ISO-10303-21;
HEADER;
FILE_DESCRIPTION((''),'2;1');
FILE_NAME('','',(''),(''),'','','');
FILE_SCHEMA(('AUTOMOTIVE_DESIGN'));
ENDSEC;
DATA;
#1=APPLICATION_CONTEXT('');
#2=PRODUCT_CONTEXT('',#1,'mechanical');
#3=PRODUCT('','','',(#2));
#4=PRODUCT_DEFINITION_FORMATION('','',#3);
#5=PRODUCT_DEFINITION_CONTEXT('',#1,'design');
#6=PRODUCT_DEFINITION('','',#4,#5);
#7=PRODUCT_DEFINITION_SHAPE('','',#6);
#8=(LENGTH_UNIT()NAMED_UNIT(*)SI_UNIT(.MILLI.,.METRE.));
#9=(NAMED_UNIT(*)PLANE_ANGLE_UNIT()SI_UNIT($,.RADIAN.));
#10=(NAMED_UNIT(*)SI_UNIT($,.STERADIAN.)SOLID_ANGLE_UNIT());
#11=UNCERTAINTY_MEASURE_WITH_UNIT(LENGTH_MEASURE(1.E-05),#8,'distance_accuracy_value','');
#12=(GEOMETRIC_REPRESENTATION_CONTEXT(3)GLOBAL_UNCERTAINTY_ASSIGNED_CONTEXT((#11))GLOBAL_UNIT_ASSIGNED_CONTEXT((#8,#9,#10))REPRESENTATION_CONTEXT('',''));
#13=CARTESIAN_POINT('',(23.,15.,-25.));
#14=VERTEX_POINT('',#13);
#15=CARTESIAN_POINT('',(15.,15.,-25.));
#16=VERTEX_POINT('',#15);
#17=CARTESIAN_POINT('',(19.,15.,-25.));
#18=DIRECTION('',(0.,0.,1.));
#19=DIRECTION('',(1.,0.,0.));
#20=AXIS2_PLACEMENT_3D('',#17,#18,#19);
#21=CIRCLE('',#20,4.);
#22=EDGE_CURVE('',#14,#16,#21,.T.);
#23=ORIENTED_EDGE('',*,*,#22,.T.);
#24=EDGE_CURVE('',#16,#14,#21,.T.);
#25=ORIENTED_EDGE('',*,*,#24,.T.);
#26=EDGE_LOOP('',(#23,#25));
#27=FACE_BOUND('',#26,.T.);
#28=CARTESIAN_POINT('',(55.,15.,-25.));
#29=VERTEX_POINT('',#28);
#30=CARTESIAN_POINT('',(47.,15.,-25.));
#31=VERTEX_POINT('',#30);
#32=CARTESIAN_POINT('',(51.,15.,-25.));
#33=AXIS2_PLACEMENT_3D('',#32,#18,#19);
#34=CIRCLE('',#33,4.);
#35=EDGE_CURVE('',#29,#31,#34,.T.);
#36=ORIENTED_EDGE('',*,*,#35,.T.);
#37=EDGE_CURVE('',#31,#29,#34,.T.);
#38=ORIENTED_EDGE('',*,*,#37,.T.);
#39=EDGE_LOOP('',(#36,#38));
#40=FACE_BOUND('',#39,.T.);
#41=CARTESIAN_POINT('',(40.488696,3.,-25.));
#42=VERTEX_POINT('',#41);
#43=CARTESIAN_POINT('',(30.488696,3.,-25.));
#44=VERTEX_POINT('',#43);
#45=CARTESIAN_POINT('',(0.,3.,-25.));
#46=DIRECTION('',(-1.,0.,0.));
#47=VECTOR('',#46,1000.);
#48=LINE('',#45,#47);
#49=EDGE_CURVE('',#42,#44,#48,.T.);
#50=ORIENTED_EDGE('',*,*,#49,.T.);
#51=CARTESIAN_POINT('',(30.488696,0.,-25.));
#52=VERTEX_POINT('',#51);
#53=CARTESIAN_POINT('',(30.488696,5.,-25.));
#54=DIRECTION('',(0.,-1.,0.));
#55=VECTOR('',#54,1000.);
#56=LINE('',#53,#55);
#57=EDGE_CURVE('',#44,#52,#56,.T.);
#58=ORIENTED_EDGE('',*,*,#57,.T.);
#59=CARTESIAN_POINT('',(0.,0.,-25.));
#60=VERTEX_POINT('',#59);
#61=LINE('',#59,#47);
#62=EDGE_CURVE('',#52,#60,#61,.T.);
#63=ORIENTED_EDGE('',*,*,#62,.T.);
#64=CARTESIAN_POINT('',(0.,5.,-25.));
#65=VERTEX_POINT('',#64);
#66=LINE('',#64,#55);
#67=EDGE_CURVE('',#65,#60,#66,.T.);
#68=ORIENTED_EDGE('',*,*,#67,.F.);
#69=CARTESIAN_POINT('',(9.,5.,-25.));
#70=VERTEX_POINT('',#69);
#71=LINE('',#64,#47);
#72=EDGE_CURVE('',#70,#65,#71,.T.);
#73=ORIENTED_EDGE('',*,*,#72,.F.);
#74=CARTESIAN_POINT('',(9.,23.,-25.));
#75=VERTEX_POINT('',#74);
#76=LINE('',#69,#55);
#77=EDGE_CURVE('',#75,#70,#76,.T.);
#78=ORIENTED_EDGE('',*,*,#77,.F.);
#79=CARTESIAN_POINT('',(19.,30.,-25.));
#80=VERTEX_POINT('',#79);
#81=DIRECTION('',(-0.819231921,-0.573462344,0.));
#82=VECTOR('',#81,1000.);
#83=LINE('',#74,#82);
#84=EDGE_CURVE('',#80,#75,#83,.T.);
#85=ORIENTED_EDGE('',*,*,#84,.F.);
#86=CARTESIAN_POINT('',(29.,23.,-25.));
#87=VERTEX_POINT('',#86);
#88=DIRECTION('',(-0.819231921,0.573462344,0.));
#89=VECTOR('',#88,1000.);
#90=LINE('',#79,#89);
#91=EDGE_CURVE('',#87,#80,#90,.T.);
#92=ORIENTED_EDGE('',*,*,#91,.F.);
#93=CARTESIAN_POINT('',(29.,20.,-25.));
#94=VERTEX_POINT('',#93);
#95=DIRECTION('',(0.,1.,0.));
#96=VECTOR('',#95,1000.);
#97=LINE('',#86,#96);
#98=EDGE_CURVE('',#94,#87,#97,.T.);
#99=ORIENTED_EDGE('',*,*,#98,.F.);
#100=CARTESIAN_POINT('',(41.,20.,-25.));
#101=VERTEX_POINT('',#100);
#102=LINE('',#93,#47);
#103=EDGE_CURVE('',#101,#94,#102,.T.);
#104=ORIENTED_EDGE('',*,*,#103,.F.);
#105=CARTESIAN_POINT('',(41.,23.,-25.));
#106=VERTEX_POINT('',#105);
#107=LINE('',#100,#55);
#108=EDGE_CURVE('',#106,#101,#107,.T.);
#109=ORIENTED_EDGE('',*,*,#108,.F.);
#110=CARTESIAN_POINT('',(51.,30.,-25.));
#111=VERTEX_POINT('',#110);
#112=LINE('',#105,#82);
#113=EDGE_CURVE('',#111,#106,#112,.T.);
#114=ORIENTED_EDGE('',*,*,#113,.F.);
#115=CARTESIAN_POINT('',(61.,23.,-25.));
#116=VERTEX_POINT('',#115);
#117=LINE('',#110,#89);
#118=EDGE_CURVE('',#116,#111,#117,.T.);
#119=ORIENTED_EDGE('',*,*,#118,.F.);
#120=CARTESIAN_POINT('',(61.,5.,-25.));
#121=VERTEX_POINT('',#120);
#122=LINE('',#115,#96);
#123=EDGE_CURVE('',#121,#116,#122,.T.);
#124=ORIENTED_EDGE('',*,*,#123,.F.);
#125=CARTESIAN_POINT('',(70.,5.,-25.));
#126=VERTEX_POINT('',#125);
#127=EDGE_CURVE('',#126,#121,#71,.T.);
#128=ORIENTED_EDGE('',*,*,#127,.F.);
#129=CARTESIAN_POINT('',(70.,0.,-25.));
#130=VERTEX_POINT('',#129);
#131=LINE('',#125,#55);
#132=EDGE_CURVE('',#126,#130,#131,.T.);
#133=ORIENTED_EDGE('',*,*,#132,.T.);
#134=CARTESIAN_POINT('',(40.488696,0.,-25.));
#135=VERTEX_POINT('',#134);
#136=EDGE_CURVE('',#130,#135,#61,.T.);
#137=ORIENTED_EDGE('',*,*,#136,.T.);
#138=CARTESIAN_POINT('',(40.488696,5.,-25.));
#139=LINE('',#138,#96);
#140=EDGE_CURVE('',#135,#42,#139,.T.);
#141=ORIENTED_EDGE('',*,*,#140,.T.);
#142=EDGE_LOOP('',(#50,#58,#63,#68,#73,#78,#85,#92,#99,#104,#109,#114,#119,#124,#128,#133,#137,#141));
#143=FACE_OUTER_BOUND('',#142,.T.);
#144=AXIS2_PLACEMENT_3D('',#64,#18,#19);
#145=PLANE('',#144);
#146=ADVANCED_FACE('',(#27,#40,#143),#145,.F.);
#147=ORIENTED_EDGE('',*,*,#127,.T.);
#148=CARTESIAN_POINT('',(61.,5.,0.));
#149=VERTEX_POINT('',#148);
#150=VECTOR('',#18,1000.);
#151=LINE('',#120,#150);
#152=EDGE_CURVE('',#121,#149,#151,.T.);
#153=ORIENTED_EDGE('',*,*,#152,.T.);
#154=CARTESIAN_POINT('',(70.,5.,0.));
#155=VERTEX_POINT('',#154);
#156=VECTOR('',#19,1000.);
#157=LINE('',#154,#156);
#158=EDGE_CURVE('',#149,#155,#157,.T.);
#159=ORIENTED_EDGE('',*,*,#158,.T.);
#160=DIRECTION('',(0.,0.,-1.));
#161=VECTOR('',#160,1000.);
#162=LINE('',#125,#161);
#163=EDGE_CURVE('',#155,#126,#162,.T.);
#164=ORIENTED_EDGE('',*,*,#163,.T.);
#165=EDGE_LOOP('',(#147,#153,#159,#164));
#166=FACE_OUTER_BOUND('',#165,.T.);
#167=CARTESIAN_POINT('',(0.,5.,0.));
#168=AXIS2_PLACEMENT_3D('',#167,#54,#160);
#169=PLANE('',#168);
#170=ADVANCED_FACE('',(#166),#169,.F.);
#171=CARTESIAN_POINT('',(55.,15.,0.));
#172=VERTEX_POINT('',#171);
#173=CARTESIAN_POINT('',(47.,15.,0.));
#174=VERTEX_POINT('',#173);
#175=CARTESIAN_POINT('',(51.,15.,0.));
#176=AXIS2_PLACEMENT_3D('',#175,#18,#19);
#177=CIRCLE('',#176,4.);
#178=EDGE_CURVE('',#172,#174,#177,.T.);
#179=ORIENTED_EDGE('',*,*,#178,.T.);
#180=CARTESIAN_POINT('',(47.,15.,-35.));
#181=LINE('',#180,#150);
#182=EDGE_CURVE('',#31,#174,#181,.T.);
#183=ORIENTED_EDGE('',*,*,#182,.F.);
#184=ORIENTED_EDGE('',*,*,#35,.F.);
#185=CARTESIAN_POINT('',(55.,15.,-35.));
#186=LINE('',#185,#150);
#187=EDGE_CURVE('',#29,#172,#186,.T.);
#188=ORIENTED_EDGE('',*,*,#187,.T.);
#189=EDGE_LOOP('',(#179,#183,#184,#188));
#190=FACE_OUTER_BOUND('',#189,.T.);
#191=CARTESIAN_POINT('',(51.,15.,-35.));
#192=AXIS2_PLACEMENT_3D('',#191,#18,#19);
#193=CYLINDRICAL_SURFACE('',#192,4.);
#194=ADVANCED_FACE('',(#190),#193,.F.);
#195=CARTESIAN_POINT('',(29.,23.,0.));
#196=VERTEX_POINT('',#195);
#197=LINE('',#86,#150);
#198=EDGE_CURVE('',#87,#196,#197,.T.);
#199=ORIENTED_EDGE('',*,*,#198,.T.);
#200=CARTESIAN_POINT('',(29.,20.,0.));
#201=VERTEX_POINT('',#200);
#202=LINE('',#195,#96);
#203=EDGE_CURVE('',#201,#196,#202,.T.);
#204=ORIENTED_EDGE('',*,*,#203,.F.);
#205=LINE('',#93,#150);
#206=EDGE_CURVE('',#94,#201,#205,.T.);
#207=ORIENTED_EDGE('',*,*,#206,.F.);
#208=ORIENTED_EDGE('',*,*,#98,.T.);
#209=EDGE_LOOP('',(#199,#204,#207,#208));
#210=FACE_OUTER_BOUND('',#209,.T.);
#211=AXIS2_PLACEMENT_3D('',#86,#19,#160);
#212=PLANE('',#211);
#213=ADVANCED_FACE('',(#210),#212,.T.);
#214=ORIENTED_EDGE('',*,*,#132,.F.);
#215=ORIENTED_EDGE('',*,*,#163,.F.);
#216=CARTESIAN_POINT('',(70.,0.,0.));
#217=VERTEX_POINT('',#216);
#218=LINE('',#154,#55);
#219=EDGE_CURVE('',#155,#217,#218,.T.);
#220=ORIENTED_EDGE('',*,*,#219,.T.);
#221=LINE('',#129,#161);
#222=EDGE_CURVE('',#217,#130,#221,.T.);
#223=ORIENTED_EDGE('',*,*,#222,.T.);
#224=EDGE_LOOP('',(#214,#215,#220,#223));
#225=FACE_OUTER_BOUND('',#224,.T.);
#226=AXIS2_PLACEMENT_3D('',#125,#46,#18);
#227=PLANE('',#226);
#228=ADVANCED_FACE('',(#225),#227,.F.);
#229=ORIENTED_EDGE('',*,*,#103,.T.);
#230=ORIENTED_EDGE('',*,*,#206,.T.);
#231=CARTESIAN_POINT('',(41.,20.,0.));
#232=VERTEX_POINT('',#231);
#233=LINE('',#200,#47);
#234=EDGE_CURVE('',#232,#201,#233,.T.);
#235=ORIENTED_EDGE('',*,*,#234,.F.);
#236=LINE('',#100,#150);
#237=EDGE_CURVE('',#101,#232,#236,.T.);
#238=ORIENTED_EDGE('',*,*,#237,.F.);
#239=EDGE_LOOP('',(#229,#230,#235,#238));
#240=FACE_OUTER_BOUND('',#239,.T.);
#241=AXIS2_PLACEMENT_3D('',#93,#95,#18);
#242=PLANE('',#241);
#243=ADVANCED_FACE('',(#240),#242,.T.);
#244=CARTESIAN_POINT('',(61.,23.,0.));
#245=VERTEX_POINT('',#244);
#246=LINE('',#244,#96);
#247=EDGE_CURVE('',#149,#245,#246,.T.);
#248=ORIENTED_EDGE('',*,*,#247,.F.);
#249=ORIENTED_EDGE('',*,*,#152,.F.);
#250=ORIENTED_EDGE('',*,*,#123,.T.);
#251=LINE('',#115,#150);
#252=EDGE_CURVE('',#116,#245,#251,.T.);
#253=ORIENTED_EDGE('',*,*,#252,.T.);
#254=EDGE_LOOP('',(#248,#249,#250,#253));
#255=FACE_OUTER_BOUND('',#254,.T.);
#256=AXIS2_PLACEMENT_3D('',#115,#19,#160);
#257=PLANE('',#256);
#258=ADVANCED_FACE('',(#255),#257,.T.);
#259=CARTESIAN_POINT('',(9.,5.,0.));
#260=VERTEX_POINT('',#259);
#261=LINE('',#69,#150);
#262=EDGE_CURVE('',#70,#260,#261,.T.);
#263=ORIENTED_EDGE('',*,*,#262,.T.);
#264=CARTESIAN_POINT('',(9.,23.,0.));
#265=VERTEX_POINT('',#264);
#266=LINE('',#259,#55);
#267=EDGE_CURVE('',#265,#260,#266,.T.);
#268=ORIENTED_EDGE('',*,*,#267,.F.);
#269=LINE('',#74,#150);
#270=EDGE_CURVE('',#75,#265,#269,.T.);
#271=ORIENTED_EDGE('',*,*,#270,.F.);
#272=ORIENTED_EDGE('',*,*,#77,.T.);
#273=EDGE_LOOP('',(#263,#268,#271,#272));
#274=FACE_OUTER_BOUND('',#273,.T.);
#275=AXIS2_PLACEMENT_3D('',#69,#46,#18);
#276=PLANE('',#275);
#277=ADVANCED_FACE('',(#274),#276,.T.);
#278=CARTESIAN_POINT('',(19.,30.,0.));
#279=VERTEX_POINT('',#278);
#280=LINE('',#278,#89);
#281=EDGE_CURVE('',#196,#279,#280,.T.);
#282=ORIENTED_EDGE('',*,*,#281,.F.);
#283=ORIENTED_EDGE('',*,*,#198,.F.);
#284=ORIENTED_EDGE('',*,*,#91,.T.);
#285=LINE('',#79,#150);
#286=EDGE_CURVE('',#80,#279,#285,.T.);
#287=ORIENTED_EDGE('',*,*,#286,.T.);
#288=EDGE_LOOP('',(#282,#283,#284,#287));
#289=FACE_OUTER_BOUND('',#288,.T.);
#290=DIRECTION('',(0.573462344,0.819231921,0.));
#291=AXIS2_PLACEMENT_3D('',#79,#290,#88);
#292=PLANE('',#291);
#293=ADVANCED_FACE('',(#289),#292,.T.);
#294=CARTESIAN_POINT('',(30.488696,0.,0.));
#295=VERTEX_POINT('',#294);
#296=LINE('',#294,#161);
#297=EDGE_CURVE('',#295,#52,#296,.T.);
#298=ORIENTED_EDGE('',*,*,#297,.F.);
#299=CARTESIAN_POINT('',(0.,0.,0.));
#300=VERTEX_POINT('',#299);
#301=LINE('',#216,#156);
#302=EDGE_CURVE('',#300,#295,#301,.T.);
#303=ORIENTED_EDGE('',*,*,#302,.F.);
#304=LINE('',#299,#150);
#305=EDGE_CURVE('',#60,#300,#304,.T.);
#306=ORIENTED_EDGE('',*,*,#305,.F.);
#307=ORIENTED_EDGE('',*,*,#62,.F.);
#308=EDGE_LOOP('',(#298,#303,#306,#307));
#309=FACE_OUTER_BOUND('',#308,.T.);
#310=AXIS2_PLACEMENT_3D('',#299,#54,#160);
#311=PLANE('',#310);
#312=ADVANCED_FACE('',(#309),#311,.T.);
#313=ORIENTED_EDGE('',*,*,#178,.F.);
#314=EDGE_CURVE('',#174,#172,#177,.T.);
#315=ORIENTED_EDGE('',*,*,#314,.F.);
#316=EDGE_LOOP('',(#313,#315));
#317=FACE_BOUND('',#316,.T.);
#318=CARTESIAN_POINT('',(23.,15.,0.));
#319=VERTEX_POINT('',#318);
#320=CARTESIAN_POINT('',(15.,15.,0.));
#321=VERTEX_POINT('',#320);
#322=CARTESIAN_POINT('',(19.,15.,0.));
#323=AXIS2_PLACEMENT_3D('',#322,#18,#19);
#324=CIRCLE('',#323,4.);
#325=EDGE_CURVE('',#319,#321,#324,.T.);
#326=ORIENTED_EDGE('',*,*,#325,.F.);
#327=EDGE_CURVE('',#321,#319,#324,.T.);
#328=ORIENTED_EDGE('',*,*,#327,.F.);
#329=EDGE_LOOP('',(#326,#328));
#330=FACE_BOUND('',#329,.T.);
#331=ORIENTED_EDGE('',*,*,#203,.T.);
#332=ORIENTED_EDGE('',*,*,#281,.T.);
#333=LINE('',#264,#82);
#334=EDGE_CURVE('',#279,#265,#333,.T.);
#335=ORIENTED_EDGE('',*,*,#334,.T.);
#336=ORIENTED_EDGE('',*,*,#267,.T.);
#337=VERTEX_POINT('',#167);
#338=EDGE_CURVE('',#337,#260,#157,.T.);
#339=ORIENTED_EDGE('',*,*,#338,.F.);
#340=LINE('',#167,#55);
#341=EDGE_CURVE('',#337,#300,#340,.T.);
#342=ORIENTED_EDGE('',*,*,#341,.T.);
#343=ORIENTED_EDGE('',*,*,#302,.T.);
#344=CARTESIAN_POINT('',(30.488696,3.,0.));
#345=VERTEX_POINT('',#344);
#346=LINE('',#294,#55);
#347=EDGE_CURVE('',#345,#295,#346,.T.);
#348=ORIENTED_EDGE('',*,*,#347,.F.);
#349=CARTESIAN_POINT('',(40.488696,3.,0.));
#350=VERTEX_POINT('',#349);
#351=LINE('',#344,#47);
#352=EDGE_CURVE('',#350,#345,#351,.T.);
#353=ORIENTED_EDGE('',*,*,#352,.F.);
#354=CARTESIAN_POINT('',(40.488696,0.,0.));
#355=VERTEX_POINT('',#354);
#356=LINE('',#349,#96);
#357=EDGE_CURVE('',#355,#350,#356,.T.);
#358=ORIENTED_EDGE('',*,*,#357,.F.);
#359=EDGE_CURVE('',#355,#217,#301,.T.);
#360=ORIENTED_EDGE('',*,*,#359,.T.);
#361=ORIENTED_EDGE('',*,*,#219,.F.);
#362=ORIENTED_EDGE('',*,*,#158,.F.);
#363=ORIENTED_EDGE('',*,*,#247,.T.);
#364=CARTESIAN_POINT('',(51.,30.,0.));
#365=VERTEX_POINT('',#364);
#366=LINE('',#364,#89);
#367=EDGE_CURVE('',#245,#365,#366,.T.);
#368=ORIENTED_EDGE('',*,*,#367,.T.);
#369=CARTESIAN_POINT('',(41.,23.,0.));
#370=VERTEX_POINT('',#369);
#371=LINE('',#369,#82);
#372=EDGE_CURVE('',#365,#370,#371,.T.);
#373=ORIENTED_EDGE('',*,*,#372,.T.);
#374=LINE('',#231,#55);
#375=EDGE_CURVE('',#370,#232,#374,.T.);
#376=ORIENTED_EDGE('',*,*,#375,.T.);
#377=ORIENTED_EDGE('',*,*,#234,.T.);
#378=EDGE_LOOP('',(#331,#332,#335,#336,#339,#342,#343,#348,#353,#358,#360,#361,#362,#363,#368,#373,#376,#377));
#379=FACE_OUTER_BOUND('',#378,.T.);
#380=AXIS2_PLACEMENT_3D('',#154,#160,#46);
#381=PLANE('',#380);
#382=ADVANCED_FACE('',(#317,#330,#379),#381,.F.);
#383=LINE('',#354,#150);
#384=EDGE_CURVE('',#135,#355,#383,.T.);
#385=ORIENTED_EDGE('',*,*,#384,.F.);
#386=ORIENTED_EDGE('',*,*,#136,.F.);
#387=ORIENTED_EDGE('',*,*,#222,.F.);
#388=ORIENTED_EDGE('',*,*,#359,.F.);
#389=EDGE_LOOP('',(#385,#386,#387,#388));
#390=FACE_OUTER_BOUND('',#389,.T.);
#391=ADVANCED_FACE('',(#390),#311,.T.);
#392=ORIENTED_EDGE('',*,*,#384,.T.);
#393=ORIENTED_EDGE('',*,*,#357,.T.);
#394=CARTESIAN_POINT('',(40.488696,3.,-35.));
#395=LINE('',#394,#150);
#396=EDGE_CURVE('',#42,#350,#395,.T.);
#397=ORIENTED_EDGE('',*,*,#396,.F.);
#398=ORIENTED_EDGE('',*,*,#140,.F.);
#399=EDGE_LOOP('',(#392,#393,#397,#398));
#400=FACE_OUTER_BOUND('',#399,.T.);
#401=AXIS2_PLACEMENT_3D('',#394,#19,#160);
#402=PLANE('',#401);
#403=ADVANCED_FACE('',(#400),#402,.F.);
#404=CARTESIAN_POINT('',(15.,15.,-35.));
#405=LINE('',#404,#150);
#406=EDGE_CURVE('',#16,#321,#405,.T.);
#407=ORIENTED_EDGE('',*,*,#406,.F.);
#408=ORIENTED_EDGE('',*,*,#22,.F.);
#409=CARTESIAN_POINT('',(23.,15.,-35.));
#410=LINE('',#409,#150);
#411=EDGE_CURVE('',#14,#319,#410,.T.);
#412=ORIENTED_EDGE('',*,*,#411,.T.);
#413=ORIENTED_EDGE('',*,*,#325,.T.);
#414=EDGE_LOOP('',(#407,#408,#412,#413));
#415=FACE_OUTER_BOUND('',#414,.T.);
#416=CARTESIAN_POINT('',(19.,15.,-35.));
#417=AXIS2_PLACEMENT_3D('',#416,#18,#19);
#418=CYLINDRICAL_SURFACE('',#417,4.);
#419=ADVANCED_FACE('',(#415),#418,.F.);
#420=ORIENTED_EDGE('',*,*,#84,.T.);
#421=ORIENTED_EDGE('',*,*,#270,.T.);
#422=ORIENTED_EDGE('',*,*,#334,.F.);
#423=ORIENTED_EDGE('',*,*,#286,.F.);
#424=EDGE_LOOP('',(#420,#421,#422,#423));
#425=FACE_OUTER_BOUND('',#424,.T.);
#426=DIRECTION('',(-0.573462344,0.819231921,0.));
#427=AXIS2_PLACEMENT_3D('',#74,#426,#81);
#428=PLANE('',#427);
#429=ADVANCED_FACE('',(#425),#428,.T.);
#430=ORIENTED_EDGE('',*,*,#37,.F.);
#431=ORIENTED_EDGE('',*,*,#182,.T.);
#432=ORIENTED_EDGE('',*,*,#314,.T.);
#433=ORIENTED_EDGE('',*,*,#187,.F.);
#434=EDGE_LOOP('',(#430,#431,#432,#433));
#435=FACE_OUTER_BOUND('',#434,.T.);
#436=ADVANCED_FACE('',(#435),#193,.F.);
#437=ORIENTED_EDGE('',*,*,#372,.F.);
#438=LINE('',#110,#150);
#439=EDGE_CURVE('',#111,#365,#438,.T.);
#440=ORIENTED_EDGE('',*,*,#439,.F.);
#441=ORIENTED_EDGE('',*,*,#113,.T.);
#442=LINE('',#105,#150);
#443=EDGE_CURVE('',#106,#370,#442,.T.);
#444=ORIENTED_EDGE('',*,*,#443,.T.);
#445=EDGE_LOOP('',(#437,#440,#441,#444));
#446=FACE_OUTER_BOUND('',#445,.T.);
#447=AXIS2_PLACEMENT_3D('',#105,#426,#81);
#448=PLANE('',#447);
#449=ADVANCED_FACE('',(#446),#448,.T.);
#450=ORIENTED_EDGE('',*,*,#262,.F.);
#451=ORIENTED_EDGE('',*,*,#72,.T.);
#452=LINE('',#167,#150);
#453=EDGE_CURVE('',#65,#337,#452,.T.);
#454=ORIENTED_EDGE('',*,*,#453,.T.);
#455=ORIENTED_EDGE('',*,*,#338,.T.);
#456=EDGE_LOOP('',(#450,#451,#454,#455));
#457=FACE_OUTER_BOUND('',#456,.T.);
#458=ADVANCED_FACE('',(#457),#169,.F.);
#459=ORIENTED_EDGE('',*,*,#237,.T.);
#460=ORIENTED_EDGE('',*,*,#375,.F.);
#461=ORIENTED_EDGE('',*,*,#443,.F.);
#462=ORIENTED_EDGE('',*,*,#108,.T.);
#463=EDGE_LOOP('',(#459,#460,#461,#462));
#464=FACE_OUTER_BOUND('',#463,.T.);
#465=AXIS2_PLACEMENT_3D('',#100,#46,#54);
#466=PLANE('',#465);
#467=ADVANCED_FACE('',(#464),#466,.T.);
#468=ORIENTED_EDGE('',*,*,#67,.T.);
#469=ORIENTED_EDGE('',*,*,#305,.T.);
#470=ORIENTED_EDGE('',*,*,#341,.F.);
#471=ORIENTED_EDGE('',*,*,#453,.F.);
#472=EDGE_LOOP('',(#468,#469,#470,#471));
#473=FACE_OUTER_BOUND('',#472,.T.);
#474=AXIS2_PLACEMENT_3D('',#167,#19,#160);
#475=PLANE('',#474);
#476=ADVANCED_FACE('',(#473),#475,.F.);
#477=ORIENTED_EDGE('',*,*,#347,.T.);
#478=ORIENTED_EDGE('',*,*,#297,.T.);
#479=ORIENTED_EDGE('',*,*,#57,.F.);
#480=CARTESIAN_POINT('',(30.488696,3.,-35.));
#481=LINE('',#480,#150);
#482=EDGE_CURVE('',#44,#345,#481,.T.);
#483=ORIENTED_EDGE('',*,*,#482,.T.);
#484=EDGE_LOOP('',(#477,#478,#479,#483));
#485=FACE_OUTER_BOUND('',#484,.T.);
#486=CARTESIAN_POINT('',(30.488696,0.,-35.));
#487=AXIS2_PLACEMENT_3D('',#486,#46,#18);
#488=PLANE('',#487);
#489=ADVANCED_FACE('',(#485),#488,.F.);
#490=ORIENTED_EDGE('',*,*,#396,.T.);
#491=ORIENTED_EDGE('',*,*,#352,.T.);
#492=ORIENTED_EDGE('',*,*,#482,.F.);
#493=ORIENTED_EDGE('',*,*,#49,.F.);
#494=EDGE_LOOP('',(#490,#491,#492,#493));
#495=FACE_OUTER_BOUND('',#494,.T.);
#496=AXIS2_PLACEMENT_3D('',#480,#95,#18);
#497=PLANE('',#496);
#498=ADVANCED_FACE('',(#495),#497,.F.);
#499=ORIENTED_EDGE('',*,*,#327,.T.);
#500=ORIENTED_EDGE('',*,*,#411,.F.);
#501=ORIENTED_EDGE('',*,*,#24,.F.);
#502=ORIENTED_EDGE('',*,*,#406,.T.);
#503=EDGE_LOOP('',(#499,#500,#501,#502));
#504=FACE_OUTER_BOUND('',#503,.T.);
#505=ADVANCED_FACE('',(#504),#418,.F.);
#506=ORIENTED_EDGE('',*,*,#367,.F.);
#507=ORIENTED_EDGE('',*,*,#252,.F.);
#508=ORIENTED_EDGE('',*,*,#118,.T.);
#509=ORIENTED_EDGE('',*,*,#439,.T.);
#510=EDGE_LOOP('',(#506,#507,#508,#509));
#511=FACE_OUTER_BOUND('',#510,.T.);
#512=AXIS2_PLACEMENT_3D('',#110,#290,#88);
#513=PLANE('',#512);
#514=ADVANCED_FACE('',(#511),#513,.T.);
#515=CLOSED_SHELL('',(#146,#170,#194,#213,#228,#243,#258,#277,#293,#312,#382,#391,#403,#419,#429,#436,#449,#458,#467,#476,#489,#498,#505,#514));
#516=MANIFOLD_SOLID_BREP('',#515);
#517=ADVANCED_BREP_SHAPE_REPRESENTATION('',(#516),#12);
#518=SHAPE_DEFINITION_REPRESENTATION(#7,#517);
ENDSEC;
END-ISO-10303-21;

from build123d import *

# Parameters (mm, degrees)
BASE_PLATE_SKETCH_W              = 70
BASE_PLATE_SKETCH_H              = 25
BASE_PLATE_70X25X5_DEPTH         = 5
TWIN_PILLARS_DEPTH               = 25
CROSS_HOLES_SKETCH_R             = 4
CROSS_HOLES_2X_8_DEPTH           = 35
RELIEF_SLOT_SKETCH_W             = 10
RELIEF_SLOT_SKETCH_H             = 3
UNDERSIDE_RELIEF_SLOT_10X3_DEPTH = 35


with BuildPart() as part:
    # Base Plate Sketch → Base Plate 70x25x5 (new body)
    with BuildSketch(Plane(origin=(0, 0, 0), x_dir=(1, 0, 0), z_dir=(0, 1, 0))):
        with Locations((35, 12.5)):
            Rectangle(BASE_PLATE_SKETCH_W, BASE_PLATE_SKETCH_H)
    extrude(amount=BASE_PLATE_70X25X5_DEPTH)

    # Pillar Profile Sketch → Twin Pillars (add)
    with BuildSketch(Plane.XY):
        Polygon((9, 5), (9, 23), (19, 30), (29, 23), (29, 20), (41, 20), (41, 23), (51, 30), (61, 23), (61, 5), align=None)
    extrude(amount=-TWIN_PILLARS_DEPTH)

    # Cross Holes Sketch → Cross Holes 2xØ8 (cut)
    with BuildSketch(Plane.XY):
        with Locations((51, 15)):
            Circle(CROSS_HOLES_SKETCH_R)
        with Locations((19, 15)):
            Circle(CROSS_HOLES_SKETCH_R)
    extrude(amount=-CROSS_HOLES_2X_8_DEPTH, mode=Mode.SUBTRACT)

    # Relief Slot Sketch → Underside Relief Slot 10x3 (cut)
    with BuildSketch(Plane.XY):
        with Locations((35.488696345, 1.5)):
            Rectangle(RELIEF_SLOT_SKETCH_W, RELIEF_SLOT_SKETCH_H)
    extrude(amount=-UNDERSIDE_RELIEF_SLOT_10X3_DEPTH, mode=Mode.SUBTRACT)


solid = part.part
